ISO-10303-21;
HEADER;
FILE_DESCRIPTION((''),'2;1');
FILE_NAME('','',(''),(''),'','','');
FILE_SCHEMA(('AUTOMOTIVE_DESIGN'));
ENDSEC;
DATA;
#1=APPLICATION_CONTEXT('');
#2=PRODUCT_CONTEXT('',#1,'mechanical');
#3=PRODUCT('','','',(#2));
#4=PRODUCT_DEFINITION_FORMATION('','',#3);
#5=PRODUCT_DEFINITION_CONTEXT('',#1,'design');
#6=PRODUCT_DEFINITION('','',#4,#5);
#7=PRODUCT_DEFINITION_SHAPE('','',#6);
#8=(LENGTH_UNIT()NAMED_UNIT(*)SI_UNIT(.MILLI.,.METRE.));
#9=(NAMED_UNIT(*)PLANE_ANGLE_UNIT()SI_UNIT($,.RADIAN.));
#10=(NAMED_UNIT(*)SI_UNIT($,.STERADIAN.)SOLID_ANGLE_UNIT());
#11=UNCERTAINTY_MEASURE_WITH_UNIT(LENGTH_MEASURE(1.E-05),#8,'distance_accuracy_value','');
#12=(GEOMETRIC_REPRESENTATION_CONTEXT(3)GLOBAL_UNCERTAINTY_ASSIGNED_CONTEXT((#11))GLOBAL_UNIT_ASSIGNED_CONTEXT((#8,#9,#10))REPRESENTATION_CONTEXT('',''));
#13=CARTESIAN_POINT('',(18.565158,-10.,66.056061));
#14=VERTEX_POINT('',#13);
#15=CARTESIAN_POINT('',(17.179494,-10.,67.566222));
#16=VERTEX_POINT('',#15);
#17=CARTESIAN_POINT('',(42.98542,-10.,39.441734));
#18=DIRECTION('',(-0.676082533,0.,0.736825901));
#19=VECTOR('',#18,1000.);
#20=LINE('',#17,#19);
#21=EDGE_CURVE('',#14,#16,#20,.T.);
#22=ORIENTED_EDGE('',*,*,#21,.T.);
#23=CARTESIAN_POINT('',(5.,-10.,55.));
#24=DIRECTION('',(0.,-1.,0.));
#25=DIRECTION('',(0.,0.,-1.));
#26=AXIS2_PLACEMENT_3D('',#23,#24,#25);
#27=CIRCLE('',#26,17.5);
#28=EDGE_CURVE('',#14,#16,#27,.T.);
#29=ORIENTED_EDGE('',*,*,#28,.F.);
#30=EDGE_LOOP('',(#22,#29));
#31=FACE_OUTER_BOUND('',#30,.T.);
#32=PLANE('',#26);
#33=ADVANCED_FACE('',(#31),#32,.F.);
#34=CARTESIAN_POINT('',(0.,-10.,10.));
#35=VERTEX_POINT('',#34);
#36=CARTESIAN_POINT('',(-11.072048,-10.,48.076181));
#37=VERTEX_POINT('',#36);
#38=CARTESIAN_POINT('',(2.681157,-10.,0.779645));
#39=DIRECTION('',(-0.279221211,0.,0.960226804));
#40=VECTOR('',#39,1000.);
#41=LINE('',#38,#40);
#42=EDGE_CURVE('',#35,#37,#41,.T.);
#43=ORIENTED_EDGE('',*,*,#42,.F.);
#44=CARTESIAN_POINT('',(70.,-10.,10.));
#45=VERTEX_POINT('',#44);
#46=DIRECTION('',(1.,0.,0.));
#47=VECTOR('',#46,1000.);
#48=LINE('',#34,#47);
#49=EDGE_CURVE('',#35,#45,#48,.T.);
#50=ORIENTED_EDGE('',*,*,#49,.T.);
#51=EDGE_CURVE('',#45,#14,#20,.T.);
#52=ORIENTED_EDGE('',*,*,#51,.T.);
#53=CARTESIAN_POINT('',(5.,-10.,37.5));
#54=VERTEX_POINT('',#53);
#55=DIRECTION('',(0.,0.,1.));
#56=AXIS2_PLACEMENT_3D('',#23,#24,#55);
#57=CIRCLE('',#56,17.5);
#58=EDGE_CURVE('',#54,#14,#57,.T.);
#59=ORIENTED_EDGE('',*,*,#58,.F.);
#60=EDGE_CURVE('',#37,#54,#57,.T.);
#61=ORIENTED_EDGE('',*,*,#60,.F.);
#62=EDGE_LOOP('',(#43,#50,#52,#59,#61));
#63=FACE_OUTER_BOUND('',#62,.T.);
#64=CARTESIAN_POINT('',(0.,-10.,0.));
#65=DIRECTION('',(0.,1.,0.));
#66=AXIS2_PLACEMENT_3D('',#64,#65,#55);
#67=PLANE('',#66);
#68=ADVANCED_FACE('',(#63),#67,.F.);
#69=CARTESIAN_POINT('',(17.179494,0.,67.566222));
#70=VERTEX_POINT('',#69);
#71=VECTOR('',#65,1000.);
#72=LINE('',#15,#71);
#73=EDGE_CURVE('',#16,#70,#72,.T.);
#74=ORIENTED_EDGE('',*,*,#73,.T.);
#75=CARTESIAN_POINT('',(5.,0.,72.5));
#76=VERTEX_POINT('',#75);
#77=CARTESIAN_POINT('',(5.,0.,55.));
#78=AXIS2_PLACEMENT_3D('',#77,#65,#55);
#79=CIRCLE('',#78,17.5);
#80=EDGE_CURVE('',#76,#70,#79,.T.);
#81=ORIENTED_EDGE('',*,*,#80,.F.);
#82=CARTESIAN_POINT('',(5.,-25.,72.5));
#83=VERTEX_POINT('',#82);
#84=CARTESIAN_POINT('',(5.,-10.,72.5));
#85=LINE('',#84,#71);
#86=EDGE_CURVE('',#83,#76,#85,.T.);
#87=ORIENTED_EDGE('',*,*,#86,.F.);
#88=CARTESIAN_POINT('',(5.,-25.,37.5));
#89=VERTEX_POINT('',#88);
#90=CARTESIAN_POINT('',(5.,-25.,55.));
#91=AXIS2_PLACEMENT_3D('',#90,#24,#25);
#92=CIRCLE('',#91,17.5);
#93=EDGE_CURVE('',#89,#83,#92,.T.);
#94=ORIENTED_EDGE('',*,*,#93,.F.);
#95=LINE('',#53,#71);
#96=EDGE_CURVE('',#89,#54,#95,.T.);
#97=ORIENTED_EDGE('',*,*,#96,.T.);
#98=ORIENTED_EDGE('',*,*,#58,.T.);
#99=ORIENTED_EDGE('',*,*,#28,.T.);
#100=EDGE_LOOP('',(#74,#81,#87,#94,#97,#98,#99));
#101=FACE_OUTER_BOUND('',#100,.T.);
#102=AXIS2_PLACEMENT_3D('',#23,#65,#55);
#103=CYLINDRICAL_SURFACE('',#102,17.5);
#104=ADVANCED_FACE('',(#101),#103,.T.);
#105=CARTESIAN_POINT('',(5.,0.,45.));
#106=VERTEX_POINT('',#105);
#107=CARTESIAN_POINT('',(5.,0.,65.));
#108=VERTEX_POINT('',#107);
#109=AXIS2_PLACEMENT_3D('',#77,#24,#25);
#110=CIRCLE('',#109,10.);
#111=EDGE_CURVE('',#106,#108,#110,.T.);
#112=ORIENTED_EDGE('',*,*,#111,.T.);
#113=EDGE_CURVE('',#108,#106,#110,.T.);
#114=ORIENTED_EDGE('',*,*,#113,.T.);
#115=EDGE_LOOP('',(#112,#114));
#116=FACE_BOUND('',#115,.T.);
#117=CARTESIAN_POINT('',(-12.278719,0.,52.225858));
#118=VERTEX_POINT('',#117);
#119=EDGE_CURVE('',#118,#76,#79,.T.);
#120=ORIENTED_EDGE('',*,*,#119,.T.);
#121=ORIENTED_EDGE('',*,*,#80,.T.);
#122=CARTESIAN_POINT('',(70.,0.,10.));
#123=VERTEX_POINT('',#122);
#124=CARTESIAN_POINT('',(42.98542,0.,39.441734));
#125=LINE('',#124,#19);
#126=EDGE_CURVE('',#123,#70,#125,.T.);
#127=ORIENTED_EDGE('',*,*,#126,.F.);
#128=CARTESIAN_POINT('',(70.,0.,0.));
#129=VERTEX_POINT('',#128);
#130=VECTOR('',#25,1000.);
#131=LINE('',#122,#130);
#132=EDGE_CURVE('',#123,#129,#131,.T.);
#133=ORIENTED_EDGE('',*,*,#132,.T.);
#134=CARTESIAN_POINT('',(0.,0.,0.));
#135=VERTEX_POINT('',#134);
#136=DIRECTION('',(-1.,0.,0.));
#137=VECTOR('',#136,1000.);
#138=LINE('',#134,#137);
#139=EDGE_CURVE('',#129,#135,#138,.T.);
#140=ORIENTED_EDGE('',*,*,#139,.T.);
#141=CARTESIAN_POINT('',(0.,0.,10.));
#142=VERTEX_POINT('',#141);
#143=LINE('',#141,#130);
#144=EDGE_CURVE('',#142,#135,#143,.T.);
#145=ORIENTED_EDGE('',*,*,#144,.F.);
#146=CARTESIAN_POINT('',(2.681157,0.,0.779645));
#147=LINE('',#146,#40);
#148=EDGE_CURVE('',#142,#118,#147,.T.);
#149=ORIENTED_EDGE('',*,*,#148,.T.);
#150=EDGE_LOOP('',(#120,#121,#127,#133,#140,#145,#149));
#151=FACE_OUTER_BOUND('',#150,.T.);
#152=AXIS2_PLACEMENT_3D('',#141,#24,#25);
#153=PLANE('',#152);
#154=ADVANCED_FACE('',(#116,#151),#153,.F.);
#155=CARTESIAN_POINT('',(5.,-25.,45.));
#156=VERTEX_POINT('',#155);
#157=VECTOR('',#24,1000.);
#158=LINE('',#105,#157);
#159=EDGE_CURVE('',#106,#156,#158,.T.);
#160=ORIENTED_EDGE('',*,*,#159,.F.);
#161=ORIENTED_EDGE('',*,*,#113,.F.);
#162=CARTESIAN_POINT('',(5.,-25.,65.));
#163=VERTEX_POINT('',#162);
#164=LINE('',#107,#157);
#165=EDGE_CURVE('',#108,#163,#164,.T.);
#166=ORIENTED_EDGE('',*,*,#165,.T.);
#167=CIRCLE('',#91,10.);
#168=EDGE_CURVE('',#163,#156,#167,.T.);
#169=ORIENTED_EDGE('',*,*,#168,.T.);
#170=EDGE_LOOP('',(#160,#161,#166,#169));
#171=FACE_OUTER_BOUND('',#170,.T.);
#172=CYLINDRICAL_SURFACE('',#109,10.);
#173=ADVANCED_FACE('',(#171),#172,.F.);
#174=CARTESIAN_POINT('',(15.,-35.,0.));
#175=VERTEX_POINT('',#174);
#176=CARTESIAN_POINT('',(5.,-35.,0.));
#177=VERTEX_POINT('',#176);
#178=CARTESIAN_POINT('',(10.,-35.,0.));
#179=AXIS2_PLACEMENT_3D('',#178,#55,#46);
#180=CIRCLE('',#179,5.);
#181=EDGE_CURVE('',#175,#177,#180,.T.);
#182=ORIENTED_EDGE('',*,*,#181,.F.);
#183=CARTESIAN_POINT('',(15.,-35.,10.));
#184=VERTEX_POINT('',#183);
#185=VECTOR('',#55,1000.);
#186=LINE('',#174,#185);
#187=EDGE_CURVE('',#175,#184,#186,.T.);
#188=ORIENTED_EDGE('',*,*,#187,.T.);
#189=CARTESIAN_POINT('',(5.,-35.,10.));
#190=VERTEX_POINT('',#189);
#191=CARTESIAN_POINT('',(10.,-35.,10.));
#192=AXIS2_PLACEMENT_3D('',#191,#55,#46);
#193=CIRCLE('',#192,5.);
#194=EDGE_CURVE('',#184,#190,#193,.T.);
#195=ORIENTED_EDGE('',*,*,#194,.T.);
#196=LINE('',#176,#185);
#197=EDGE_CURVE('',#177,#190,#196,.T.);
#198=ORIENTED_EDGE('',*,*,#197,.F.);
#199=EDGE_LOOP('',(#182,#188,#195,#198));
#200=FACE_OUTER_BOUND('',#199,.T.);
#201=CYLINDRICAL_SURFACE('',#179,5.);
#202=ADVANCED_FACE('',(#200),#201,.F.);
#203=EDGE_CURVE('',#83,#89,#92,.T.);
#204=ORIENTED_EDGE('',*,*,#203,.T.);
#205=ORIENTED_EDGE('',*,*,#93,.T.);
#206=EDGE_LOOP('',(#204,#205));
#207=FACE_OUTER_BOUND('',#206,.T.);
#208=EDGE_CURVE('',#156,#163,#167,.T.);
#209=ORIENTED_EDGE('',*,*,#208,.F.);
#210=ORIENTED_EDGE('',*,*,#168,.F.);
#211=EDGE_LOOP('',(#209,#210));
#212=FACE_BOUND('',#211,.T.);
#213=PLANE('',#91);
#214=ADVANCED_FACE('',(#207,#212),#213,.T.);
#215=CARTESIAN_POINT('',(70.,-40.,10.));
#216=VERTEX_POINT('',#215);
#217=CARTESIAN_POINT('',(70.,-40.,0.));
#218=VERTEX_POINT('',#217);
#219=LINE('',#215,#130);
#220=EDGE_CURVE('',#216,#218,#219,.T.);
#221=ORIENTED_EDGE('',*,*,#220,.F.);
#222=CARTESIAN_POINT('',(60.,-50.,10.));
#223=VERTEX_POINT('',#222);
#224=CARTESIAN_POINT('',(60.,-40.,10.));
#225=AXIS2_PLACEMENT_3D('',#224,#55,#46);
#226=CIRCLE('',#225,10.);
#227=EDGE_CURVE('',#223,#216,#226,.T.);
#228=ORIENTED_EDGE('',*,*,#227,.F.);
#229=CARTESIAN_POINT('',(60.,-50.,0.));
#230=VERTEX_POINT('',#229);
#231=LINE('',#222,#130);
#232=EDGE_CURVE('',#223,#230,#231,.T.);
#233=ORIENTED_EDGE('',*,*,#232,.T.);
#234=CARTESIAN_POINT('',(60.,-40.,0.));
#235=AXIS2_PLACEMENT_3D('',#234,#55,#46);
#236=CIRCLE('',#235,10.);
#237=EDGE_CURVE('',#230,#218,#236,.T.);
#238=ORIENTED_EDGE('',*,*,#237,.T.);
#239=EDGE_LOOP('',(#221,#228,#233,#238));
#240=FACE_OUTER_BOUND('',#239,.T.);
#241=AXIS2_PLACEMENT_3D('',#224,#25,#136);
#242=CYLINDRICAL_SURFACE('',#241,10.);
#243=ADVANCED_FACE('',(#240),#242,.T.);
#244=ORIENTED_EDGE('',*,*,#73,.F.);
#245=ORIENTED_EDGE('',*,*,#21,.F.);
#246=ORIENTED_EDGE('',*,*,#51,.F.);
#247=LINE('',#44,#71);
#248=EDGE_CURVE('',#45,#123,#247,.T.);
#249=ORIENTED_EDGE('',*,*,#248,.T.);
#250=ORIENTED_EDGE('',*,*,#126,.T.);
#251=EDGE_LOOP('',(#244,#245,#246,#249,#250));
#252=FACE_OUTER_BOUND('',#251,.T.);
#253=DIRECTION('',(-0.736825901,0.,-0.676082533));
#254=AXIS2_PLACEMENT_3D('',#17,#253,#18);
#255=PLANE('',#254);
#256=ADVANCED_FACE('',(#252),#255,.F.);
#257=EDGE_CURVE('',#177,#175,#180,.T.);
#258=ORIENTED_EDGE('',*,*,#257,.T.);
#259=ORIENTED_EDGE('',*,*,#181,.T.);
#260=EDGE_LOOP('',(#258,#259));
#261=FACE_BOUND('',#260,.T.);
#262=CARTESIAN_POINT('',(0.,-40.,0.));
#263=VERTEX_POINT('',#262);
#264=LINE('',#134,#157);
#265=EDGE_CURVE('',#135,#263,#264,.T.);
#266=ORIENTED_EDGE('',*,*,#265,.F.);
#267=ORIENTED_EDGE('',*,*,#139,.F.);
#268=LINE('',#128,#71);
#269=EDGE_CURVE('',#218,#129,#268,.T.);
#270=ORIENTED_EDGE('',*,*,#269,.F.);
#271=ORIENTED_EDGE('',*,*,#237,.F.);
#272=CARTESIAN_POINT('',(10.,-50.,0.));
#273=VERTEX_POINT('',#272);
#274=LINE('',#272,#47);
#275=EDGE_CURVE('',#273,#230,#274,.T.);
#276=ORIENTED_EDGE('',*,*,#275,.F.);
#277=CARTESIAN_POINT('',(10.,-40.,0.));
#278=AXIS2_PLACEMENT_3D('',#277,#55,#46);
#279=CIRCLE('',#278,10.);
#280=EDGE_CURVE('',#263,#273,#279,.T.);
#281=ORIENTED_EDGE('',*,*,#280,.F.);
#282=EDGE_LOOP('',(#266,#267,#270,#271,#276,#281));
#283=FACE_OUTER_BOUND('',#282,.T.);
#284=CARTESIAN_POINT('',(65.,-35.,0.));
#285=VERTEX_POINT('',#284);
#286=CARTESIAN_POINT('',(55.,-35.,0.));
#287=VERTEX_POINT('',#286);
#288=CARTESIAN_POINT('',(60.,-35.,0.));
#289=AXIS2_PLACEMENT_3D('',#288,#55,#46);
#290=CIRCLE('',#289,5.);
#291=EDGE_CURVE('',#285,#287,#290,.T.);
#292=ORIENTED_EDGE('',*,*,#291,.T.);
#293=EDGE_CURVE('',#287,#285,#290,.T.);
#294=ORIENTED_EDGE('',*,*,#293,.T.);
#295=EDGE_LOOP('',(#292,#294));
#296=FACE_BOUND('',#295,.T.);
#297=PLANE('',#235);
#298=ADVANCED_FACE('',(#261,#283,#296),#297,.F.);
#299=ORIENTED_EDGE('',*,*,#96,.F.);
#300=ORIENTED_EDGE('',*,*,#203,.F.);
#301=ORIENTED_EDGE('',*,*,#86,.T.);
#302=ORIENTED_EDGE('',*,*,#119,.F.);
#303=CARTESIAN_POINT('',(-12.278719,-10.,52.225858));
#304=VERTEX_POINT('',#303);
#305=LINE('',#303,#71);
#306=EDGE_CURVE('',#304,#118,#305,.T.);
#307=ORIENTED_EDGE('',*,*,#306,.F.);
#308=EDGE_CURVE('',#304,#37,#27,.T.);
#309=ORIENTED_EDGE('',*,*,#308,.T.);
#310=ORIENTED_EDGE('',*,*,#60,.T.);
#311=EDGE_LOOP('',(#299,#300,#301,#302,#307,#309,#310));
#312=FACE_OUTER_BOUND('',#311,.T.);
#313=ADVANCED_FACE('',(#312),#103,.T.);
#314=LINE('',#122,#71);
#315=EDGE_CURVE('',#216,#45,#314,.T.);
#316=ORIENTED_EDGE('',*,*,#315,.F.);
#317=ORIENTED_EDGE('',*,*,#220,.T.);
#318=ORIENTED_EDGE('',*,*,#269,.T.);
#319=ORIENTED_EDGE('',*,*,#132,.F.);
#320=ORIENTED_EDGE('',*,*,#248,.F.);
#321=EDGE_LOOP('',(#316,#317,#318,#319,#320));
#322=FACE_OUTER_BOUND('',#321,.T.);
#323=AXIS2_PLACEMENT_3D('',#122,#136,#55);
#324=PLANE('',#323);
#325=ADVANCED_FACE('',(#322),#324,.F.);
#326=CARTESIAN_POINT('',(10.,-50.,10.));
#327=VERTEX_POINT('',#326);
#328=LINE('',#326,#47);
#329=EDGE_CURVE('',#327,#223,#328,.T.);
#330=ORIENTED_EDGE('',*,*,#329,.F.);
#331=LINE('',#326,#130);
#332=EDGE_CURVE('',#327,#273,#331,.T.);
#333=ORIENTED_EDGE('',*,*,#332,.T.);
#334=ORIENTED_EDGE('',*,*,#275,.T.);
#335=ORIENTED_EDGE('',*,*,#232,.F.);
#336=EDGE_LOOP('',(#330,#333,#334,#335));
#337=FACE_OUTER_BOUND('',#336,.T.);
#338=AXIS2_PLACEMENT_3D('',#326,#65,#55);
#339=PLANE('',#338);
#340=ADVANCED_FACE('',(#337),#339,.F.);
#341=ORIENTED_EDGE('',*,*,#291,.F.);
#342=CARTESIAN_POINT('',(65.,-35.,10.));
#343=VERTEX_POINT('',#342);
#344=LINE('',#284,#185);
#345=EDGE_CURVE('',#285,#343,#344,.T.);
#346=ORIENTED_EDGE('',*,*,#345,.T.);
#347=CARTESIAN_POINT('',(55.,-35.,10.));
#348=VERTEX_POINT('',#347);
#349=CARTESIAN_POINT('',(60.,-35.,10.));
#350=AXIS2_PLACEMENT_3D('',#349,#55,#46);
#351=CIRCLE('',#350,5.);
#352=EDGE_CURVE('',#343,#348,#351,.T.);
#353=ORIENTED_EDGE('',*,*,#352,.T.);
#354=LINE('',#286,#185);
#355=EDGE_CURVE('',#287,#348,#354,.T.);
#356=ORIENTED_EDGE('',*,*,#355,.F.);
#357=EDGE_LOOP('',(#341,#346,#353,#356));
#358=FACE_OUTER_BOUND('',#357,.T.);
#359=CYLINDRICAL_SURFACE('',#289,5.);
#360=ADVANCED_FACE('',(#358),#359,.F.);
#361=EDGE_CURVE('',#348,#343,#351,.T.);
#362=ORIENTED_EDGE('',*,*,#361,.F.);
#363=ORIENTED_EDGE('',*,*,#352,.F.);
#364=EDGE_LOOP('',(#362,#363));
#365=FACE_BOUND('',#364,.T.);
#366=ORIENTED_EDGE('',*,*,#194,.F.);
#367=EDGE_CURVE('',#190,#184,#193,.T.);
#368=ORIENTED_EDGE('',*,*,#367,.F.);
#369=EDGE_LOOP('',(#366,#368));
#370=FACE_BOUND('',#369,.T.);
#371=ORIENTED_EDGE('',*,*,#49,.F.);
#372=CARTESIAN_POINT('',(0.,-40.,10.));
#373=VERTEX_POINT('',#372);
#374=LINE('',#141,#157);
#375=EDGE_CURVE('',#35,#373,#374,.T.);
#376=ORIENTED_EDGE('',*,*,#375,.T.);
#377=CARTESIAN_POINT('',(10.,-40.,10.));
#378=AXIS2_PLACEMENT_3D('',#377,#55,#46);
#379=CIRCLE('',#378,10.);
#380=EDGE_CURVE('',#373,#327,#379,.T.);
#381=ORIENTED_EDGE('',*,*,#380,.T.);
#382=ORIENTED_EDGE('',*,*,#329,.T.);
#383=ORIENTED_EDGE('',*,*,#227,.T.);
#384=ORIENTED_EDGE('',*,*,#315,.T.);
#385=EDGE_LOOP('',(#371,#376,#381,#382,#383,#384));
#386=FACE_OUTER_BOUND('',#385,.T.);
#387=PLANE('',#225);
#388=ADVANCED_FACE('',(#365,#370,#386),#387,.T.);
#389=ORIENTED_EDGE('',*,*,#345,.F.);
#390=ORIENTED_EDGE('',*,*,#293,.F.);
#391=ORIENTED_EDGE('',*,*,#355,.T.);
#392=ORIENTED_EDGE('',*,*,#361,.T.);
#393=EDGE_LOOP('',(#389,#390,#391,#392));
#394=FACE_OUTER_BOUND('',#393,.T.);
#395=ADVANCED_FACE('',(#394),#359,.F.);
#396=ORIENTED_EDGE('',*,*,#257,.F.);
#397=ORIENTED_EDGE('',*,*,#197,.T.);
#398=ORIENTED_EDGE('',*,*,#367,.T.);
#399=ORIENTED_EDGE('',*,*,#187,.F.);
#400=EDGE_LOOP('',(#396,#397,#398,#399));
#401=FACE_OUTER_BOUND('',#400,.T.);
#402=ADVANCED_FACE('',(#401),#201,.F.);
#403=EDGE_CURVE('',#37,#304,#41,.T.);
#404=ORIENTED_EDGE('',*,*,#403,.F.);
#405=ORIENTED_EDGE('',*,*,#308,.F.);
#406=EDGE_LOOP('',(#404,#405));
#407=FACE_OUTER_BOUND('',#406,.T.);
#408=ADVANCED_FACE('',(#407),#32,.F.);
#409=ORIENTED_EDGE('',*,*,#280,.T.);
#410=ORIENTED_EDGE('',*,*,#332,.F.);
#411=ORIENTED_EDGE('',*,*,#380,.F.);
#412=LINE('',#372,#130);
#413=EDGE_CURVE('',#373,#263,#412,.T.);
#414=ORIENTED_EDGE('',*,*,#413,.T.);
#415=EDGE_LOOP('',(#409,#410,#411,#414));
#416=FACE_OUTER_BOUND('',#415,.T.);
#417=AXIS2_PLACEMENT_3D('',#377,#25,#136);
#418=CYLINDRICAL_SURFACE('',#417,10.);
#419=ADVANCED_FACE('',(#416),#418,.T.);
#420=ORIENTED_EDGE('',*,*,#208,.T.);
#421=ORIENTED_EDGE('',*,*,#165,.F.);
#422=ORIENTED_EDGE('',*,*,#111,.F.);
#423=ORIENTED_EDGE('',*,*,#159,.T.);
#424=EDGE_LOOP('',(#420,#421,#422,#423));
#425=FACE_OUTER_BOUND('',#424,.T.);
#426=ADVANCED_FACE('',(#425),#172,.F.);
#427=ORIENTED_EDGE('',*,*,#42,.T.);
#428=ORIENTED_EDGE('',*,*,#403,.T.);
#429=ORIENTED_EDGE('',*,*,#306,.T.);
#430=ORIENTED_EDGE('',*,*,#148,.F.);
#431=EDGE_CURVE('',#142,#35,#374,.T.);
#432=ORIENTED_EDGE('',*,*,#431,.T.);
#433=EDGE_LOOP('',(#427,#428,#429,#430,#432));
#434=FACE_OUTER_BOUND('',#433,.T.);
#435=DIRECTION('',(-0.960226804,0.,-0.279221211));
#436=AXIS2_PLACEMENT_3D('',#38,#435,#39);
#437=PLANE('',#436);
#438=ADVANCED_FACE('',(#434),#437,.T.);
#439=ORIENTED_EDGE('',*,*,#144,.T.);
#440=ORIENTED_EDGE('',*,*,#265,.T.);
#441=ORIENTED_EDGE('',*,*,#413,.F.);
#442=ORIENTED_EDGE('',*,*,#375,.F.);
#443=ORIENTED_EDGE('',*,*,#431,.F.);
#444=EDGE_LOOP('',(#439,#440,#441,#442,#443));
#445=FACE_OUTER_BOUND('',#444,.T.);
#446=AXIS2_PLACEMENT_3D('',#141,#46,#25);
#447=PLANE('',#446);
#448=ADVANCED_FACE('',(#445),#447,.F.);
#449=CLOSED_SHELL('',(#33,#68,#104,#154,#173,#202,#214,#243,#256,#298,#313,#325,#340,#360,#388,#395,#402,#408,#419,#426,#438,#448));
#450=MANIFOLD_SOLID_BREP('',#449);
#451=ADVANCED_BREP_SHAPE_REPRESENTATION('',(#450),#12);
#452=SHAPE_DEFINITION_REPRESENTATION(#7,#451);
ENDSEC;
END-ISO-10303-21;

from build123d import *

# Parameters (mm, degrees)
BASE_PLATE_DEPTH         = 10
SIDE_PLATE_DEPTH         = 10
HUB_BOSS_SKETCH_R        = 17.5
HUB_BOSS_35_DEPTH        = 15
HUB_BORE_SKETCH_R        = 10
HUB_BORE_20_DEPTH        = 25
SIDE_PLATE_HOLE_SKETCH_R = 5
SIDE_PLATE_HOLE_DEPTH    = 10


with BuildPart() as part:
    # Base Plate Sketch → Base Plate (new body)
    with BuildSketch(Plane.XY):
        with BuildLine():
            Line((0, 0), (0, -40))
            ThreePointArc((0, -40), (2.928932188, -47.071067812), (10, -50))
            Line((10, -50), (60, -50))
            ThreePointArc((60, -50), (67.071067812, -47.071067812), (70, -40))
            Line((70, -40), (70, 0))
            Line((70, 0), (0, 0))
        make_face()
    extrude(amount=BASE_PLATE_DEPTH)

    # Side Plate Sketch → Side Plate (add)
    with BuildSketch(Plane(origin=(0, 0, 0), x_dir=(1, 0, 0), z_dir=(0, 1, 0))):
        with BuildLine():
            Line((18.565158101, -66.056061039), (70, -10))
            Line((70, -10), (0, -10))
            Line((0, -10), (-11.072048142, -48.076181073))
            ThreePointArc((-11.072048142, -48.076181073), (8.534767144, -37.860705346), (22.5, -55))
            ThreePointArc((22.5, -55), (21.486968593, -60.867696875), (18.565158101, -66.056061039))
        make_face()
        with BuildLine():
            Line((17.179494078, -67.566221548), (18.565158101, -66.056061039))
            ThreePointArc((18.565158101, -66.056061039), (21.486968593, -60.867696875), (22.5, -55))
            ThreePointArc((22.5, -55), (8.534767144, -37.860705346), (-11.072048142, -48.076181073))
            Line((-11.072048142, -48.076181073), (-12.278719231, -52.225858378))
            ThreePointArc((-12.278719231, -52.225858378), (-3.08283427, -70.52152667), (17.179494078, -67.566221548))
        make_face()
    extrude(amount=-SIDE_PLATE_DEPTH)

    # Hub Boss Sketch → Hub Boss Ø35 (add)
    with BuildSketch(Plane.XZ.offset(10)):
        with Locations(Location((5, 55, 0), (0, 0, 45.895348857))):
            Circle(HUB_BOSS_SKETCH_R)
    extrude(amount=HUB_BOSS_35_DEPTH)

    # Hub Bore Sketch → Hub Bore Ø20 (cut)
    with BuildSketch(Plane.XZ.offset(25)):
        with Locations(Location((5, 55, 0), (0, 0, 270))):
            Circle(HUB_BORE_SKETCH_R)
    extrude(amount=-HUB_BORE_20_DEPTH, mode=Mode.SUBTRACT)

    # Side Plate Hole Sketch → Side Plate Hole (cut)
    with BuildSketch(Plane.XY.offset(10)):
        with Locations((10, -35)):
            Circle(SIDE_PLATE_HOLE_SKETCH_R)
        with Locations((60, -35)):
            Circle(SIDE_PLATE_HOLE_SKETCH_R)
    extrude(amount=-SIDE_PLATE_HOLE_DEPTH, mode=Mode.SUBTRACT)


solid = part.part
